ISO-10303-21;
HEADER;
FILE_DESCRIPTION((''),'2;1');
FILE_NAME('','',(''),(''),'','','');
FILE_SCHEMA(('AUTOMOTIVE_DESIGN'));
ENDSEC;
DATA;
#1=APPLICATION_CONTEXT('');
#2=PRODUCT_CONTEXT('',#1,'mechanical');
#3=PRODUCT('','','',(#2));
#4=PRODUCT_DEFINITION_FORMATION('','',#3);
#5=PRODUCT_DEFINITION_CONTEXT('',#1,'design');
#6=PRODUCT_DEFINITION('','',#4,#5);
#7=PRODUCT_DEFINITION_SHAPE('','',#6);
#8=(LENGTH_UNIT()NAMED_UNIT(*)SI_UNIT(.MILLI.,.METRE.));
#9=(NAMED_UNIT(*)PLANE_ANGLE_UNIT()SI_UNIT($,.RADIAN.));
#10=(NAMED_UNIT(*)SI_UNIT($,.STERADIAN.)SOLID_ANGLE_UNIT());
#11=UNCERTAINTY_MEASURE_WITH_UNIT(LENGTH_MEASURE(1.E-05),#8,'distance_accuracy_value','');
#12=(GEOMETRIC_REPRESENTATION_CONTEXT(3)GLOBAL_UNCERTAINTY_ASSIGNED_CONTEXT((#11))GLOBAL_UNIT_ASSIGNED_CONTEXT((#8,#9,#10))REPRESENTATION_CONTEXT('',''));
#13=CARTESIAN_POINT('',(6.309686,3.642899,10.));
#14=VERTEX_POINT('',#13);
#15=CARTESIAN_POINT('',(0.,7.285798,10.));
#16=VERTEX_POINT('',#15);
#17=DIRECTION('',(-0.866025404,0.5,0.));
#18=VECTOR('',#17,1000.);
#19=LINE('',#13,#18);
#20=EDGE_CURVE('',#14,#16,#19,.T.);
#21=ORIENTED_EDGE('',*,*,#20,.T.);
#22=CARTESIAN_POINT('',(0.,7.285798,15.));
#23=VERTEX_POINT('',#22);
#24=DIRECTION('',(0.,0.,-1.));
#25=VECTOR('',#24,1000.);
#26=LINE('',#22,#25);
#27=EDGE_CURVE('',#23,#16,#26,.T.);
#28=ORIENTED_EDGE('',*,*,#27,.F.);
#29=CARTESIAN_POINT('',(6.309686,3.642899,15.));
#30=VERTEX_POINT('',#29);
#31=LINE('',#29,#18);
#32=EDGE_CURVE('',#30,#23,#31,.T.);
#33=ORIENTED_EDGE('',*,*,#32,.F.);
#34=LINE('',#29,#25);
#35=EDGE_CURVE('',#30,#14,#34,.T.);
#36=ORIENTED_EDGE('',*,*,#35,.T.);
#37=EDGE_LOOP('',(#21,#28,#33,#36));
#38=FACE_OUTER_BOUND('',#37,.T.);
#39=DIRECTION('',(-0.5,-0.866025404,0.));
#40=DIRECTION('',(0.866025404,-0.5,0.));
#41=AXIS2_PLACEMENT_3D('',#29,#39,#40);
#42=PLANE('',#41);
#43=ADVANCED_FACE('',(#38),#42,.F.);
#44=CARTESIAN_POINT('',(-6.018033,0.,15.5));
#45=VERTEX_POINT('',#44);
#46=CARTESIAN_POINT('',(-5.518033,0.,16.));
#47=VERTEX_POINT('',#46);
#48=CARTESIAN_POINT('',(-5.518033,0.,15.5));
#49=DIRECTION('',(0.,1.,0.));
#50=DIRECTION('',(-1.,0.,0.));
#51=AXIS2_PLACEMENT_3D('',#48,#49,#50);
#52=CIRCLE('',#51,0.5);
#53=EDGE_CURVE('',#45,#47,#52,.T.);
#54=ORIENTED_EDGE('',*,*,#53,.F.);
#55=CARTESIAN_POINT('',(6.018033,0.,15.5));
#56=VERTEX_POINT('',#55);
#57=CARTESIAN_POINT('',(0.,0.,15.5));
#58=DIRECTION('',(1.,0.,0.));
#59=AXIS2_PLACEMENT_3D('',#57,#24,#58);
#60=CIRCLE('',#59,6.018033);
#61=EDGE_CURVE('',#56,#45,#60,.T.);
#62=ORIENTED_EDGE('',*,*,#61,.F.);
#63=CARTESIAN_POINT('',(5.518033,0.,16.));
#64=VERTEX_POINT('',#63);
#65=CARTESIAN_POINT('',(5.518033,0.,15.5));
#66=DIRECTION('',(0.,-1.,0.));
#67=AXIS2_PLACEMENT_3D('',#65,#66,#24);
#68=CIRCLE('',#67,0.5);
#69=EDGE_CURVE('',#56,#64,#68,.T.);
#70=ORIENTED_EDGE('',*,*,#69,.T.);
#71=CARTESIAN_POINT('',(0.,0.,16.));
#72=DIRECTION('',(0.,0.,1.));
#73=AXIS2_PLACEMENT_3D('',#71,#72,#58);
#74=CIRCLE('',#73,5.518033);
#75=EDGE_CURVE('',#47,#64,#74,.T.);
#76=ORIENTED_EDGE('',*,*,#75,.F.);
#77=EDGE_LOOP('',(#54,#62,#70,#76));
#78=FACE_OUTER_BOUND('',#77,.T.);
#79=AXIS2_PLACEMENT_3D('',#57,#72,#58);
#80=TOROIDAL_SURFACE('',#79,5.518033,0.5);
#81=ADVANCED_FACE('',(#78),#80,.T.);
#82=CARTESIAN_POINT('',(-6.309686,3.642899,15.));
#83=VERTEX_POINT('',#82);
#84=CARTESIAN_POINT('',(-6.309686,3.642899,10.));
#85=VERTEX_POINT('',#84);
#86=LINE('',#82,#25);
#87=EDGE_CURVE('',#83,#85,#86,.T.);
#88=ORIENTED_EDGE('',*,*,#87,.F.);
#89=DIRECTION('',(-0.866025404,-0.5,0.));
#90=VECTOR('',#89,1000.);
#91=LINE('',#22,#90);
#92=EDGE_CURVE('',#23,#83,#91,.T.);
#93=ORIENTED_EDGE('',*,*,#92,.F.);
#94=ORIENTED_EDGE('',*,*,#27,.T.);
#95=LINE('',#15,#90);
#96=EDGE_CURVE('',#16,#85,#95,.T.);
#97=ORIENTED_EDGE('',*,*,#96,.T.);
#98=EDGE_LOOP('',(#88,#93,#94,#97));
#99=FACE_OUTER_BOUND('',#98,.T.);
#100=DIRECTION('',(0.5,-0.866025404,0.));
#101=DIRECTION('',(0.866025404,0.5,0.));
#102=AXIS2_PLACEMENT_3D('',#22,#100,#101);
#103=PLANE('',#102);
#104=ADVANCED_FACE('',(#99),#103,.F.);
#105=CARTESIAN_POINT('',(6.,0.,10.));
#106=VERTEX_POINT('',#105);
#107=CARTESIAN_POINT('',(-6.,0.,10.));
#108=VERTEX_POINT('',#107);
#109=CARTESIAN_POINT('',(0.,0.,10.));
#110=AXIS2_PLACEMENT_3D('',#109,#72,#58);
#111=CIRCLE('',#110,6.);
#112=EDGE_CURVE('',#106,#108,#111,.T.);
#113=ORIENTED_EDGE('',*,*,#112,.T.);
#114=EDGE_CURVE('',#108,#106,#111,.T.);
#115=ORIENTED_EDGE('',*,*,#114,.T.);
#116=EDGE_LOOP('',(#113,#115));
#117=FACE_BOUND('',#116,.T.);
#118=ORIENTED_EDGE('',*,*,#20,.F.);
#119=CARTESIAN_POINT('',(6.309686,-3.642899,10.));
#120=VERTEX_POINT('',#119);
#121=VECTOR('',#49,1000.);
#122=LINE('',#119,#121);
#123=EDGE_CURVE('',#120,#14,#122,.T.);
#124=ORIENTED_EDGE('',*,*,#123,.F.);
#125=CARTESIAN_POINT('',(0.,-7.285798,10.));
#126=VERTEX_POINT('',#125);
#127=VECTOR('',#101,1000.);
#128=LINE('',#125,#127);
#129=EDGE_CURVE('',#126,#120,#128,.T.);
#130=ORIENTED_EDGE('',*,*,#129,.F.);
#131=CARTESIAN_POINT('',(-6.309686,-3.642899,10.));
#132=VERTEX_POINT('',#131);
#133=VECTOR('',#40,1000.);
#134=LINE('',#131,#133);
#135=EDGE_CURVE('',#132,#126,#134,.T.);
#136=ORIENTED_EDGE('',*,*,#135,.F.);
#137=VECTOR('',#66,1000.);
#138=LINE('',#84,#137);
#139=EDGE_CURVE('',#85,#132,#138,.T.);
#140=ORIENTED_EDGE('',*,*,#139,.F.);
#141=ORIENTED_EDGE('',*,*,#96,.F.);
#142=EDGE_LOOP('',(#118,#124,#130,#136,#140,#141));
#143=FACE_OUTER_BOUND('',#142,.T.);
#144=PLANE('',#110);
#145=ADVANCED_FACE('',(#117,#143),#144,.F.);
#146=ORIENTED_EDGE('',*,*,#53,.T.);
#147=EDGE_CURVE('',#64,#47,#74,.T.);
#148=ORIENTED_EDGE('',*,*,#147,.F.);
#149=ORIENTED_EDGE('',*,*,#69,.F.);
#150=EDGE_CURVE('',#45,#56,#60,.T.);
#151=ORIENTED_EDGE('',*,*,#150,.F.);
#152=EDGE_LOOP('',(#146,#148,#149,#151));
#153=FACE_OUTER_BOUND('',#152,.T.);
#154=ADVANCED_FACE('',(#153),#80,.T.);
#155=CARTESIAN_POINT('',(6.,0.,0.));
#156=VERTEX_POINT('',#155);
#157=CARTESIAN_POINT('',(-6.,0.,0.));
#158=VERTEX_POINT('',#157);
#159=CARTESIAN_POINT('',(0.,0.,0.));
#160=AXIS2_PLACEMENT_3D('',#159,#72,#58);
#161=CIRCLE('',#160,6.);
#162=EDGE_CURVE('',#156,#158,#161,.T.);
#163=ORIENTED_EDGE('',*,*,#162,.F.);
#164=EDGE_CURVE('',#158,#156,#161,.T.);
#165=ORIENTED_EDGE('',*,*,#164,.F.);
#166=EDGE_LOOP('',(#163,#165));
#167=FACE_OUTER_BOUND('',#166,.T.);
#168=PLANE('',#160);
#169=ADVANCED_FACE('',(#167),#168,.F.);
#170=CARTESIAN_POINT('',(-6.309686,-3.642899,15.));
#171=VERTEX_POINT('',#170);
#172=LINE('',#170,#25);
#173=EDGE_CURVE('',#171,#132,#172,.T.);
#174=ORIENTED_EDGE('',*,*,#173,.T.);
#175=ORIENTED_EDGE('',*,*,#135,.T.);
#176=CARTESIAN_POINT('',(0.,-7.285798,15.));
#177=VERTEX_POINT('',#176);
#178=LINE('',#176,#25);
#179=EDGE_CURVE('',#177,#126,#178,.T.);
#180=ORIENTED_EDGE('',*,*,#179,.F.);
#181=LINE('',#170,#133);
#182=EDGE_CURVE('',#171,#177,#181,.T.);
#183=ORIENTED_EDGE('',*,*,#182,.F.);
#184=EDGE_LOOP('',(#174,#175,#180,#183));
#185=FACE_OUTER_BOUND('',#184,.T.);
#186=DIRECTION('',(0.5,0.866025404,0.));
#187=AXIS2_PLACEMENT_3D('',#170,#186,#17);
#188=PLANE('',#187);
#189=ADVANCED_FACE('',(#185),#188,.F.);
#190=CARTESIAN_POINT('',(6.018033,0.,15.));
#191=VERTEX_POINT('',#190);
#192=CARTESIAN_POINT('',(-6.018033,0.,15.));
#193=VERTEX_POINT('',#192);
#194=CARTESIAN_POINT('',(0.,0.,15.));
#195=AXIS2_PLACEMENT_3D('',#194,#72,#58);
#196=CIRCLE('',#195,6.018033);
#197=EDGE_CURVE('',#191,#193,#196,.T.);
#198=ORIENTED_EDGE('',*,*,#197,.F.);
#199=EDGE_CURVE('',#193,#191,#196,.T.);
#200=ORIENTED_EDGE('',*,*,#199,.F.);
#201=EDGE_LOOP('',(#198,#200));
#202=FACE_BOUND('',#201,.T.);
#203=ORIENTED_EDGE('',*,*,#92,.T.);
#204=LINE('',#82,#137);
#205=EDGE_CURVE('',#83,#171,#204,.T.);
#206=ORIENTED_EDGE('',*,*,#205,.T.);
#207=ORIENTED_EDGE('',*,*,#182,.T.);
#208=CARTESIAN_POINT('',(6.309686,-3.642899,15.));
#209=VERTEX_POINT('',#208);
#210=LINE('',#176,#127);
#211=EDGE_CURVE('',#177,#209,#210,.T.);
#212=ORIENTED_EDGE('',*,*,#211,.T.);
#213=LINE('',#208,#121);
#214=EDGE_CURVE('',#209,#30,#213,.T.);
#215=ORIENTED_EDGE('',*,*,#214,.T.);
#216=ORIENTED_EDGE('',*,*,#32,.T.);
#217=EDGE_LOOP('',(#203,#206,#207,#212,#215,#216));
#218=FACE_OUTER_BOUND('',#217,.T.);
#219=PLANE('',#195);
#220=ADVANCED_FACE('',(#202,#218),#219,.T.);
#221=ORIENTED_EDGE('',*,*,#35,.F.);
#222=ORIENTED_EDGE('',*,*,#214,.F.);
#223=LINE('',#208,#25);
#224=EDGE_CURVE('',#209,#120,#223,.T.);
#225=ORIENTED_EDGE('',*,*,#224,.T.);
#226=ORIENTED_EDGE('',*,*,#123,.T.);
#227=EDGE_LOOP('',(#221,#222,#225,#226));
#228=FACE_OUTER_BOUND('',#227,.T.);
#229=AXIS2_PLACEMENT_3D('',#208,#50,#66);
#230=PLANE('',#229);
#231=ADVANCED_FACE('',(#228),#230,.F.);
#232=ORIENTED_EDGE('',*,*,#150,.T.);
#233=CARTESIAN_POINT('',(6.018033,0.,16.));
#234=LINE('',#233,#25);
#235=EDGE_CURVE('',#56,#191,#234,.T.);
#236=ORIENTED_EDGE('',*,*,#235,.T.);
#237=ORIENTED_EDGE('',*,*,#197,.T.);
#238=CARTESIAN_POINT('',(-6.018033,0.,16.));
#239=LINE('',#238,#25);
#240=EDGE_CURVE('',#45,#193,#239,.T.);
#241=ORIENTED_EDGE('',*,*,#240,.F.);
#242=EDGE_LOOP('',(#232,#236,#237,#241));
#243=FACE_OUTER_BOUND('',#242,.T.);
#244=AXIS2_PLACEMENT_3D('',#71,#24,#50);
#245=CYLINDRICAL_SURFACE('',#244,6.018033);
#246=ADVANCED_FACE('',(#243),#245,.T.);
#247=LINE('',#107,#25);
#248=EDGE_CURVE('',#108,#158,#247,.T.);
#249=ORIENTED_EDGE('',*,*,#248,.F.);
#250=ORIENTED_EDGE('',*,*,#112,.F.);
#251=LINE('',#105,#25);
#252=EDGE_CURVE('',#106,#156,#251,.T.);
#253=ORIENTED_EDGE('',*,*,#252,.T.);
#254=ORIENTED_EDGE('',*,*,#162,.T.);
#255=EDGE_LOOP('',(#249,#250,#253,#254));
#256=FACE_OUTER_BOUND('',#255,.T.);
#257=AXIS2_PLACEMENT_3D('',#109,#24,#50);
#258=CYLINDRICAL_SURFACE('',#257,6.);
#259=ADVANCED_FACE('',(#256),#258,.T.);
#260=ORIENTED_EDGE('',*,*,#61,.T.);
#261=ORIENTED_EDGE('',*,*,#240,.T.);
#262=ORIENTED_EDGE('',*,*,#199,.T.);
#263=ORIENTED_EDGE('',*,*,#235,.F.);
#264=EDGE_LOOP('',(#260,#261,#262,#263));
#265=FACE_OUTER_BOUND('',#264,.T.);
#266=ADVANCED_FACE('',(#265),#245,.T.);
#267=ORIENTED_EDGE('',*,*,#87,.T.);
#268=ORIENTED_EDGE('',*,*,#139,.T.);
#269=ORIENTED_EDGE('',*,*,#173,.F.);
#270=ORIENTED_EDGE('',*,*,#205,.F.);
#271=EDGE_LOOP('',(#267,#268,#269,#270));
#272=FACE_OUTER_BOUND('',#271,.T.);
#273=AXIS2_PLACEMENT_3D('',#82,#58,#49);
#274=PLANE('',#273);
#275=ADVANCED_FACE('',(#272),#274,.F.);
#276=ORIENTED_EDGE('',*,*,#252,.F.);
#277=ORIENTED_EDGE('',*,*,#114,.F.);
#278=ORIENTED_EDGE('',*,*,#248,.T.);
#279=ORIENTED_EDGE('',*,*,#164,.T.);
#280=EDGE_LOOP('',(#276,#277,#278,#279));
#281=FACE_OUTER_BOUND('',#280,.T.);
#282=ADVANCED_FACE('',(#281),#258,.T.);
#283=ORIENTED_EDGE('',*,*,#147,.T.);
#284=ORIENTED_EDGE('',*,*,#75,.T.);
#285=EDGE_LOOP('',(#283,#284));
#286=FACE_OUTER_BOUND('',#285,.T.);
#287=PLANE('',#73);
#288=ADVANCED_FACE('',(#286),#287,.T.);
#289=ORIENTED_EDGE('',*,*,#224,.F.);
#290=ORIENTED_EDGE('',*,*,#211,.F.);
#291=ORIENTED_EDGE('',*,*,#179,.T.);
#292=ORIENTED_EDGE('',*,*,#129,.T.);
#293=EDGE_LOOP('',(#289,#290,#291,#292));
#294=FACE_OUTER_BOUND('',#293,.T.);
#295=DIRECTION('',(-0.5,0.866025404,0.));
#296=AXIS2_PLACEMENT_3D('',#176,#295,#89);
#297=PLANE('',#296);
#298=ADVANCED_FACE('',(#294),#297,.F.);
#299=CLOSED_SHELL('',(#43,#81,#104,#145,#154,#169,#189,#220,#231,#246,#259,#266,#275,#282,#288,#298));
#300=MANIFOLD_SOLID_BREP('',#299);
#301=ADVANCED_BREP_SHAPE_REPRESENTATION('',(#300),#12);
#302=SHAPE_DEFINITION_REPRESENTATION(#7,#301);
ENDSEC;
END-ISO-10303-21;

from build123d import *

# Parameters (mm, degrees)
SKETCH1_R           = 6
BOSS_EXTRUDE1_DEPTH = 10
BOSS_EXTRUDE2_DEPTH = 5
SKETCH3_R           = 6.018032789
BOSS_EXTRUDE3_DEPTH = 1
FILLET2_R           = 0.5


with BuildPart() as part:
    # Sketch1 → Boss-Extrude1 (new body)
    with BuildSketch(Plane.XY):
        Circle(SKETCH1_R)
    extrude(amount=BOSS_EXTRUDE1_DEPTH)

    # Sketch2 → Boss-Extrude2 (add)
    with BuildSketch(Plane.XY.offset(10)):
        Polygon((0, 7.285798141), (-6.309686277, 3.64289907), (-6.309686277, -3.64289907), (0, -7.285798141), (6.309686277, -3.64289907), (6.309686277, 3.64289907), align=None)
    extrude(amount=BOSS_EXTRUDE2_DEPTH)

    # Sketch3 → Boss-Extrude3 (add)
    with BuildSketch(Plane.XY.offset(15)):
        Circle(SKETCH3_R)
    extrude(amount=BOSS_EXTRUDE3_DEPTH)

    # Fillet2
    fillet2_edges = [part.edges().sort_by_distance(p)[0] for p in [
        (-6.018032789, 0, 16),
    ]]
    fillet(fillet2_edges, radius=FILLET2_R)


solid = part.part
